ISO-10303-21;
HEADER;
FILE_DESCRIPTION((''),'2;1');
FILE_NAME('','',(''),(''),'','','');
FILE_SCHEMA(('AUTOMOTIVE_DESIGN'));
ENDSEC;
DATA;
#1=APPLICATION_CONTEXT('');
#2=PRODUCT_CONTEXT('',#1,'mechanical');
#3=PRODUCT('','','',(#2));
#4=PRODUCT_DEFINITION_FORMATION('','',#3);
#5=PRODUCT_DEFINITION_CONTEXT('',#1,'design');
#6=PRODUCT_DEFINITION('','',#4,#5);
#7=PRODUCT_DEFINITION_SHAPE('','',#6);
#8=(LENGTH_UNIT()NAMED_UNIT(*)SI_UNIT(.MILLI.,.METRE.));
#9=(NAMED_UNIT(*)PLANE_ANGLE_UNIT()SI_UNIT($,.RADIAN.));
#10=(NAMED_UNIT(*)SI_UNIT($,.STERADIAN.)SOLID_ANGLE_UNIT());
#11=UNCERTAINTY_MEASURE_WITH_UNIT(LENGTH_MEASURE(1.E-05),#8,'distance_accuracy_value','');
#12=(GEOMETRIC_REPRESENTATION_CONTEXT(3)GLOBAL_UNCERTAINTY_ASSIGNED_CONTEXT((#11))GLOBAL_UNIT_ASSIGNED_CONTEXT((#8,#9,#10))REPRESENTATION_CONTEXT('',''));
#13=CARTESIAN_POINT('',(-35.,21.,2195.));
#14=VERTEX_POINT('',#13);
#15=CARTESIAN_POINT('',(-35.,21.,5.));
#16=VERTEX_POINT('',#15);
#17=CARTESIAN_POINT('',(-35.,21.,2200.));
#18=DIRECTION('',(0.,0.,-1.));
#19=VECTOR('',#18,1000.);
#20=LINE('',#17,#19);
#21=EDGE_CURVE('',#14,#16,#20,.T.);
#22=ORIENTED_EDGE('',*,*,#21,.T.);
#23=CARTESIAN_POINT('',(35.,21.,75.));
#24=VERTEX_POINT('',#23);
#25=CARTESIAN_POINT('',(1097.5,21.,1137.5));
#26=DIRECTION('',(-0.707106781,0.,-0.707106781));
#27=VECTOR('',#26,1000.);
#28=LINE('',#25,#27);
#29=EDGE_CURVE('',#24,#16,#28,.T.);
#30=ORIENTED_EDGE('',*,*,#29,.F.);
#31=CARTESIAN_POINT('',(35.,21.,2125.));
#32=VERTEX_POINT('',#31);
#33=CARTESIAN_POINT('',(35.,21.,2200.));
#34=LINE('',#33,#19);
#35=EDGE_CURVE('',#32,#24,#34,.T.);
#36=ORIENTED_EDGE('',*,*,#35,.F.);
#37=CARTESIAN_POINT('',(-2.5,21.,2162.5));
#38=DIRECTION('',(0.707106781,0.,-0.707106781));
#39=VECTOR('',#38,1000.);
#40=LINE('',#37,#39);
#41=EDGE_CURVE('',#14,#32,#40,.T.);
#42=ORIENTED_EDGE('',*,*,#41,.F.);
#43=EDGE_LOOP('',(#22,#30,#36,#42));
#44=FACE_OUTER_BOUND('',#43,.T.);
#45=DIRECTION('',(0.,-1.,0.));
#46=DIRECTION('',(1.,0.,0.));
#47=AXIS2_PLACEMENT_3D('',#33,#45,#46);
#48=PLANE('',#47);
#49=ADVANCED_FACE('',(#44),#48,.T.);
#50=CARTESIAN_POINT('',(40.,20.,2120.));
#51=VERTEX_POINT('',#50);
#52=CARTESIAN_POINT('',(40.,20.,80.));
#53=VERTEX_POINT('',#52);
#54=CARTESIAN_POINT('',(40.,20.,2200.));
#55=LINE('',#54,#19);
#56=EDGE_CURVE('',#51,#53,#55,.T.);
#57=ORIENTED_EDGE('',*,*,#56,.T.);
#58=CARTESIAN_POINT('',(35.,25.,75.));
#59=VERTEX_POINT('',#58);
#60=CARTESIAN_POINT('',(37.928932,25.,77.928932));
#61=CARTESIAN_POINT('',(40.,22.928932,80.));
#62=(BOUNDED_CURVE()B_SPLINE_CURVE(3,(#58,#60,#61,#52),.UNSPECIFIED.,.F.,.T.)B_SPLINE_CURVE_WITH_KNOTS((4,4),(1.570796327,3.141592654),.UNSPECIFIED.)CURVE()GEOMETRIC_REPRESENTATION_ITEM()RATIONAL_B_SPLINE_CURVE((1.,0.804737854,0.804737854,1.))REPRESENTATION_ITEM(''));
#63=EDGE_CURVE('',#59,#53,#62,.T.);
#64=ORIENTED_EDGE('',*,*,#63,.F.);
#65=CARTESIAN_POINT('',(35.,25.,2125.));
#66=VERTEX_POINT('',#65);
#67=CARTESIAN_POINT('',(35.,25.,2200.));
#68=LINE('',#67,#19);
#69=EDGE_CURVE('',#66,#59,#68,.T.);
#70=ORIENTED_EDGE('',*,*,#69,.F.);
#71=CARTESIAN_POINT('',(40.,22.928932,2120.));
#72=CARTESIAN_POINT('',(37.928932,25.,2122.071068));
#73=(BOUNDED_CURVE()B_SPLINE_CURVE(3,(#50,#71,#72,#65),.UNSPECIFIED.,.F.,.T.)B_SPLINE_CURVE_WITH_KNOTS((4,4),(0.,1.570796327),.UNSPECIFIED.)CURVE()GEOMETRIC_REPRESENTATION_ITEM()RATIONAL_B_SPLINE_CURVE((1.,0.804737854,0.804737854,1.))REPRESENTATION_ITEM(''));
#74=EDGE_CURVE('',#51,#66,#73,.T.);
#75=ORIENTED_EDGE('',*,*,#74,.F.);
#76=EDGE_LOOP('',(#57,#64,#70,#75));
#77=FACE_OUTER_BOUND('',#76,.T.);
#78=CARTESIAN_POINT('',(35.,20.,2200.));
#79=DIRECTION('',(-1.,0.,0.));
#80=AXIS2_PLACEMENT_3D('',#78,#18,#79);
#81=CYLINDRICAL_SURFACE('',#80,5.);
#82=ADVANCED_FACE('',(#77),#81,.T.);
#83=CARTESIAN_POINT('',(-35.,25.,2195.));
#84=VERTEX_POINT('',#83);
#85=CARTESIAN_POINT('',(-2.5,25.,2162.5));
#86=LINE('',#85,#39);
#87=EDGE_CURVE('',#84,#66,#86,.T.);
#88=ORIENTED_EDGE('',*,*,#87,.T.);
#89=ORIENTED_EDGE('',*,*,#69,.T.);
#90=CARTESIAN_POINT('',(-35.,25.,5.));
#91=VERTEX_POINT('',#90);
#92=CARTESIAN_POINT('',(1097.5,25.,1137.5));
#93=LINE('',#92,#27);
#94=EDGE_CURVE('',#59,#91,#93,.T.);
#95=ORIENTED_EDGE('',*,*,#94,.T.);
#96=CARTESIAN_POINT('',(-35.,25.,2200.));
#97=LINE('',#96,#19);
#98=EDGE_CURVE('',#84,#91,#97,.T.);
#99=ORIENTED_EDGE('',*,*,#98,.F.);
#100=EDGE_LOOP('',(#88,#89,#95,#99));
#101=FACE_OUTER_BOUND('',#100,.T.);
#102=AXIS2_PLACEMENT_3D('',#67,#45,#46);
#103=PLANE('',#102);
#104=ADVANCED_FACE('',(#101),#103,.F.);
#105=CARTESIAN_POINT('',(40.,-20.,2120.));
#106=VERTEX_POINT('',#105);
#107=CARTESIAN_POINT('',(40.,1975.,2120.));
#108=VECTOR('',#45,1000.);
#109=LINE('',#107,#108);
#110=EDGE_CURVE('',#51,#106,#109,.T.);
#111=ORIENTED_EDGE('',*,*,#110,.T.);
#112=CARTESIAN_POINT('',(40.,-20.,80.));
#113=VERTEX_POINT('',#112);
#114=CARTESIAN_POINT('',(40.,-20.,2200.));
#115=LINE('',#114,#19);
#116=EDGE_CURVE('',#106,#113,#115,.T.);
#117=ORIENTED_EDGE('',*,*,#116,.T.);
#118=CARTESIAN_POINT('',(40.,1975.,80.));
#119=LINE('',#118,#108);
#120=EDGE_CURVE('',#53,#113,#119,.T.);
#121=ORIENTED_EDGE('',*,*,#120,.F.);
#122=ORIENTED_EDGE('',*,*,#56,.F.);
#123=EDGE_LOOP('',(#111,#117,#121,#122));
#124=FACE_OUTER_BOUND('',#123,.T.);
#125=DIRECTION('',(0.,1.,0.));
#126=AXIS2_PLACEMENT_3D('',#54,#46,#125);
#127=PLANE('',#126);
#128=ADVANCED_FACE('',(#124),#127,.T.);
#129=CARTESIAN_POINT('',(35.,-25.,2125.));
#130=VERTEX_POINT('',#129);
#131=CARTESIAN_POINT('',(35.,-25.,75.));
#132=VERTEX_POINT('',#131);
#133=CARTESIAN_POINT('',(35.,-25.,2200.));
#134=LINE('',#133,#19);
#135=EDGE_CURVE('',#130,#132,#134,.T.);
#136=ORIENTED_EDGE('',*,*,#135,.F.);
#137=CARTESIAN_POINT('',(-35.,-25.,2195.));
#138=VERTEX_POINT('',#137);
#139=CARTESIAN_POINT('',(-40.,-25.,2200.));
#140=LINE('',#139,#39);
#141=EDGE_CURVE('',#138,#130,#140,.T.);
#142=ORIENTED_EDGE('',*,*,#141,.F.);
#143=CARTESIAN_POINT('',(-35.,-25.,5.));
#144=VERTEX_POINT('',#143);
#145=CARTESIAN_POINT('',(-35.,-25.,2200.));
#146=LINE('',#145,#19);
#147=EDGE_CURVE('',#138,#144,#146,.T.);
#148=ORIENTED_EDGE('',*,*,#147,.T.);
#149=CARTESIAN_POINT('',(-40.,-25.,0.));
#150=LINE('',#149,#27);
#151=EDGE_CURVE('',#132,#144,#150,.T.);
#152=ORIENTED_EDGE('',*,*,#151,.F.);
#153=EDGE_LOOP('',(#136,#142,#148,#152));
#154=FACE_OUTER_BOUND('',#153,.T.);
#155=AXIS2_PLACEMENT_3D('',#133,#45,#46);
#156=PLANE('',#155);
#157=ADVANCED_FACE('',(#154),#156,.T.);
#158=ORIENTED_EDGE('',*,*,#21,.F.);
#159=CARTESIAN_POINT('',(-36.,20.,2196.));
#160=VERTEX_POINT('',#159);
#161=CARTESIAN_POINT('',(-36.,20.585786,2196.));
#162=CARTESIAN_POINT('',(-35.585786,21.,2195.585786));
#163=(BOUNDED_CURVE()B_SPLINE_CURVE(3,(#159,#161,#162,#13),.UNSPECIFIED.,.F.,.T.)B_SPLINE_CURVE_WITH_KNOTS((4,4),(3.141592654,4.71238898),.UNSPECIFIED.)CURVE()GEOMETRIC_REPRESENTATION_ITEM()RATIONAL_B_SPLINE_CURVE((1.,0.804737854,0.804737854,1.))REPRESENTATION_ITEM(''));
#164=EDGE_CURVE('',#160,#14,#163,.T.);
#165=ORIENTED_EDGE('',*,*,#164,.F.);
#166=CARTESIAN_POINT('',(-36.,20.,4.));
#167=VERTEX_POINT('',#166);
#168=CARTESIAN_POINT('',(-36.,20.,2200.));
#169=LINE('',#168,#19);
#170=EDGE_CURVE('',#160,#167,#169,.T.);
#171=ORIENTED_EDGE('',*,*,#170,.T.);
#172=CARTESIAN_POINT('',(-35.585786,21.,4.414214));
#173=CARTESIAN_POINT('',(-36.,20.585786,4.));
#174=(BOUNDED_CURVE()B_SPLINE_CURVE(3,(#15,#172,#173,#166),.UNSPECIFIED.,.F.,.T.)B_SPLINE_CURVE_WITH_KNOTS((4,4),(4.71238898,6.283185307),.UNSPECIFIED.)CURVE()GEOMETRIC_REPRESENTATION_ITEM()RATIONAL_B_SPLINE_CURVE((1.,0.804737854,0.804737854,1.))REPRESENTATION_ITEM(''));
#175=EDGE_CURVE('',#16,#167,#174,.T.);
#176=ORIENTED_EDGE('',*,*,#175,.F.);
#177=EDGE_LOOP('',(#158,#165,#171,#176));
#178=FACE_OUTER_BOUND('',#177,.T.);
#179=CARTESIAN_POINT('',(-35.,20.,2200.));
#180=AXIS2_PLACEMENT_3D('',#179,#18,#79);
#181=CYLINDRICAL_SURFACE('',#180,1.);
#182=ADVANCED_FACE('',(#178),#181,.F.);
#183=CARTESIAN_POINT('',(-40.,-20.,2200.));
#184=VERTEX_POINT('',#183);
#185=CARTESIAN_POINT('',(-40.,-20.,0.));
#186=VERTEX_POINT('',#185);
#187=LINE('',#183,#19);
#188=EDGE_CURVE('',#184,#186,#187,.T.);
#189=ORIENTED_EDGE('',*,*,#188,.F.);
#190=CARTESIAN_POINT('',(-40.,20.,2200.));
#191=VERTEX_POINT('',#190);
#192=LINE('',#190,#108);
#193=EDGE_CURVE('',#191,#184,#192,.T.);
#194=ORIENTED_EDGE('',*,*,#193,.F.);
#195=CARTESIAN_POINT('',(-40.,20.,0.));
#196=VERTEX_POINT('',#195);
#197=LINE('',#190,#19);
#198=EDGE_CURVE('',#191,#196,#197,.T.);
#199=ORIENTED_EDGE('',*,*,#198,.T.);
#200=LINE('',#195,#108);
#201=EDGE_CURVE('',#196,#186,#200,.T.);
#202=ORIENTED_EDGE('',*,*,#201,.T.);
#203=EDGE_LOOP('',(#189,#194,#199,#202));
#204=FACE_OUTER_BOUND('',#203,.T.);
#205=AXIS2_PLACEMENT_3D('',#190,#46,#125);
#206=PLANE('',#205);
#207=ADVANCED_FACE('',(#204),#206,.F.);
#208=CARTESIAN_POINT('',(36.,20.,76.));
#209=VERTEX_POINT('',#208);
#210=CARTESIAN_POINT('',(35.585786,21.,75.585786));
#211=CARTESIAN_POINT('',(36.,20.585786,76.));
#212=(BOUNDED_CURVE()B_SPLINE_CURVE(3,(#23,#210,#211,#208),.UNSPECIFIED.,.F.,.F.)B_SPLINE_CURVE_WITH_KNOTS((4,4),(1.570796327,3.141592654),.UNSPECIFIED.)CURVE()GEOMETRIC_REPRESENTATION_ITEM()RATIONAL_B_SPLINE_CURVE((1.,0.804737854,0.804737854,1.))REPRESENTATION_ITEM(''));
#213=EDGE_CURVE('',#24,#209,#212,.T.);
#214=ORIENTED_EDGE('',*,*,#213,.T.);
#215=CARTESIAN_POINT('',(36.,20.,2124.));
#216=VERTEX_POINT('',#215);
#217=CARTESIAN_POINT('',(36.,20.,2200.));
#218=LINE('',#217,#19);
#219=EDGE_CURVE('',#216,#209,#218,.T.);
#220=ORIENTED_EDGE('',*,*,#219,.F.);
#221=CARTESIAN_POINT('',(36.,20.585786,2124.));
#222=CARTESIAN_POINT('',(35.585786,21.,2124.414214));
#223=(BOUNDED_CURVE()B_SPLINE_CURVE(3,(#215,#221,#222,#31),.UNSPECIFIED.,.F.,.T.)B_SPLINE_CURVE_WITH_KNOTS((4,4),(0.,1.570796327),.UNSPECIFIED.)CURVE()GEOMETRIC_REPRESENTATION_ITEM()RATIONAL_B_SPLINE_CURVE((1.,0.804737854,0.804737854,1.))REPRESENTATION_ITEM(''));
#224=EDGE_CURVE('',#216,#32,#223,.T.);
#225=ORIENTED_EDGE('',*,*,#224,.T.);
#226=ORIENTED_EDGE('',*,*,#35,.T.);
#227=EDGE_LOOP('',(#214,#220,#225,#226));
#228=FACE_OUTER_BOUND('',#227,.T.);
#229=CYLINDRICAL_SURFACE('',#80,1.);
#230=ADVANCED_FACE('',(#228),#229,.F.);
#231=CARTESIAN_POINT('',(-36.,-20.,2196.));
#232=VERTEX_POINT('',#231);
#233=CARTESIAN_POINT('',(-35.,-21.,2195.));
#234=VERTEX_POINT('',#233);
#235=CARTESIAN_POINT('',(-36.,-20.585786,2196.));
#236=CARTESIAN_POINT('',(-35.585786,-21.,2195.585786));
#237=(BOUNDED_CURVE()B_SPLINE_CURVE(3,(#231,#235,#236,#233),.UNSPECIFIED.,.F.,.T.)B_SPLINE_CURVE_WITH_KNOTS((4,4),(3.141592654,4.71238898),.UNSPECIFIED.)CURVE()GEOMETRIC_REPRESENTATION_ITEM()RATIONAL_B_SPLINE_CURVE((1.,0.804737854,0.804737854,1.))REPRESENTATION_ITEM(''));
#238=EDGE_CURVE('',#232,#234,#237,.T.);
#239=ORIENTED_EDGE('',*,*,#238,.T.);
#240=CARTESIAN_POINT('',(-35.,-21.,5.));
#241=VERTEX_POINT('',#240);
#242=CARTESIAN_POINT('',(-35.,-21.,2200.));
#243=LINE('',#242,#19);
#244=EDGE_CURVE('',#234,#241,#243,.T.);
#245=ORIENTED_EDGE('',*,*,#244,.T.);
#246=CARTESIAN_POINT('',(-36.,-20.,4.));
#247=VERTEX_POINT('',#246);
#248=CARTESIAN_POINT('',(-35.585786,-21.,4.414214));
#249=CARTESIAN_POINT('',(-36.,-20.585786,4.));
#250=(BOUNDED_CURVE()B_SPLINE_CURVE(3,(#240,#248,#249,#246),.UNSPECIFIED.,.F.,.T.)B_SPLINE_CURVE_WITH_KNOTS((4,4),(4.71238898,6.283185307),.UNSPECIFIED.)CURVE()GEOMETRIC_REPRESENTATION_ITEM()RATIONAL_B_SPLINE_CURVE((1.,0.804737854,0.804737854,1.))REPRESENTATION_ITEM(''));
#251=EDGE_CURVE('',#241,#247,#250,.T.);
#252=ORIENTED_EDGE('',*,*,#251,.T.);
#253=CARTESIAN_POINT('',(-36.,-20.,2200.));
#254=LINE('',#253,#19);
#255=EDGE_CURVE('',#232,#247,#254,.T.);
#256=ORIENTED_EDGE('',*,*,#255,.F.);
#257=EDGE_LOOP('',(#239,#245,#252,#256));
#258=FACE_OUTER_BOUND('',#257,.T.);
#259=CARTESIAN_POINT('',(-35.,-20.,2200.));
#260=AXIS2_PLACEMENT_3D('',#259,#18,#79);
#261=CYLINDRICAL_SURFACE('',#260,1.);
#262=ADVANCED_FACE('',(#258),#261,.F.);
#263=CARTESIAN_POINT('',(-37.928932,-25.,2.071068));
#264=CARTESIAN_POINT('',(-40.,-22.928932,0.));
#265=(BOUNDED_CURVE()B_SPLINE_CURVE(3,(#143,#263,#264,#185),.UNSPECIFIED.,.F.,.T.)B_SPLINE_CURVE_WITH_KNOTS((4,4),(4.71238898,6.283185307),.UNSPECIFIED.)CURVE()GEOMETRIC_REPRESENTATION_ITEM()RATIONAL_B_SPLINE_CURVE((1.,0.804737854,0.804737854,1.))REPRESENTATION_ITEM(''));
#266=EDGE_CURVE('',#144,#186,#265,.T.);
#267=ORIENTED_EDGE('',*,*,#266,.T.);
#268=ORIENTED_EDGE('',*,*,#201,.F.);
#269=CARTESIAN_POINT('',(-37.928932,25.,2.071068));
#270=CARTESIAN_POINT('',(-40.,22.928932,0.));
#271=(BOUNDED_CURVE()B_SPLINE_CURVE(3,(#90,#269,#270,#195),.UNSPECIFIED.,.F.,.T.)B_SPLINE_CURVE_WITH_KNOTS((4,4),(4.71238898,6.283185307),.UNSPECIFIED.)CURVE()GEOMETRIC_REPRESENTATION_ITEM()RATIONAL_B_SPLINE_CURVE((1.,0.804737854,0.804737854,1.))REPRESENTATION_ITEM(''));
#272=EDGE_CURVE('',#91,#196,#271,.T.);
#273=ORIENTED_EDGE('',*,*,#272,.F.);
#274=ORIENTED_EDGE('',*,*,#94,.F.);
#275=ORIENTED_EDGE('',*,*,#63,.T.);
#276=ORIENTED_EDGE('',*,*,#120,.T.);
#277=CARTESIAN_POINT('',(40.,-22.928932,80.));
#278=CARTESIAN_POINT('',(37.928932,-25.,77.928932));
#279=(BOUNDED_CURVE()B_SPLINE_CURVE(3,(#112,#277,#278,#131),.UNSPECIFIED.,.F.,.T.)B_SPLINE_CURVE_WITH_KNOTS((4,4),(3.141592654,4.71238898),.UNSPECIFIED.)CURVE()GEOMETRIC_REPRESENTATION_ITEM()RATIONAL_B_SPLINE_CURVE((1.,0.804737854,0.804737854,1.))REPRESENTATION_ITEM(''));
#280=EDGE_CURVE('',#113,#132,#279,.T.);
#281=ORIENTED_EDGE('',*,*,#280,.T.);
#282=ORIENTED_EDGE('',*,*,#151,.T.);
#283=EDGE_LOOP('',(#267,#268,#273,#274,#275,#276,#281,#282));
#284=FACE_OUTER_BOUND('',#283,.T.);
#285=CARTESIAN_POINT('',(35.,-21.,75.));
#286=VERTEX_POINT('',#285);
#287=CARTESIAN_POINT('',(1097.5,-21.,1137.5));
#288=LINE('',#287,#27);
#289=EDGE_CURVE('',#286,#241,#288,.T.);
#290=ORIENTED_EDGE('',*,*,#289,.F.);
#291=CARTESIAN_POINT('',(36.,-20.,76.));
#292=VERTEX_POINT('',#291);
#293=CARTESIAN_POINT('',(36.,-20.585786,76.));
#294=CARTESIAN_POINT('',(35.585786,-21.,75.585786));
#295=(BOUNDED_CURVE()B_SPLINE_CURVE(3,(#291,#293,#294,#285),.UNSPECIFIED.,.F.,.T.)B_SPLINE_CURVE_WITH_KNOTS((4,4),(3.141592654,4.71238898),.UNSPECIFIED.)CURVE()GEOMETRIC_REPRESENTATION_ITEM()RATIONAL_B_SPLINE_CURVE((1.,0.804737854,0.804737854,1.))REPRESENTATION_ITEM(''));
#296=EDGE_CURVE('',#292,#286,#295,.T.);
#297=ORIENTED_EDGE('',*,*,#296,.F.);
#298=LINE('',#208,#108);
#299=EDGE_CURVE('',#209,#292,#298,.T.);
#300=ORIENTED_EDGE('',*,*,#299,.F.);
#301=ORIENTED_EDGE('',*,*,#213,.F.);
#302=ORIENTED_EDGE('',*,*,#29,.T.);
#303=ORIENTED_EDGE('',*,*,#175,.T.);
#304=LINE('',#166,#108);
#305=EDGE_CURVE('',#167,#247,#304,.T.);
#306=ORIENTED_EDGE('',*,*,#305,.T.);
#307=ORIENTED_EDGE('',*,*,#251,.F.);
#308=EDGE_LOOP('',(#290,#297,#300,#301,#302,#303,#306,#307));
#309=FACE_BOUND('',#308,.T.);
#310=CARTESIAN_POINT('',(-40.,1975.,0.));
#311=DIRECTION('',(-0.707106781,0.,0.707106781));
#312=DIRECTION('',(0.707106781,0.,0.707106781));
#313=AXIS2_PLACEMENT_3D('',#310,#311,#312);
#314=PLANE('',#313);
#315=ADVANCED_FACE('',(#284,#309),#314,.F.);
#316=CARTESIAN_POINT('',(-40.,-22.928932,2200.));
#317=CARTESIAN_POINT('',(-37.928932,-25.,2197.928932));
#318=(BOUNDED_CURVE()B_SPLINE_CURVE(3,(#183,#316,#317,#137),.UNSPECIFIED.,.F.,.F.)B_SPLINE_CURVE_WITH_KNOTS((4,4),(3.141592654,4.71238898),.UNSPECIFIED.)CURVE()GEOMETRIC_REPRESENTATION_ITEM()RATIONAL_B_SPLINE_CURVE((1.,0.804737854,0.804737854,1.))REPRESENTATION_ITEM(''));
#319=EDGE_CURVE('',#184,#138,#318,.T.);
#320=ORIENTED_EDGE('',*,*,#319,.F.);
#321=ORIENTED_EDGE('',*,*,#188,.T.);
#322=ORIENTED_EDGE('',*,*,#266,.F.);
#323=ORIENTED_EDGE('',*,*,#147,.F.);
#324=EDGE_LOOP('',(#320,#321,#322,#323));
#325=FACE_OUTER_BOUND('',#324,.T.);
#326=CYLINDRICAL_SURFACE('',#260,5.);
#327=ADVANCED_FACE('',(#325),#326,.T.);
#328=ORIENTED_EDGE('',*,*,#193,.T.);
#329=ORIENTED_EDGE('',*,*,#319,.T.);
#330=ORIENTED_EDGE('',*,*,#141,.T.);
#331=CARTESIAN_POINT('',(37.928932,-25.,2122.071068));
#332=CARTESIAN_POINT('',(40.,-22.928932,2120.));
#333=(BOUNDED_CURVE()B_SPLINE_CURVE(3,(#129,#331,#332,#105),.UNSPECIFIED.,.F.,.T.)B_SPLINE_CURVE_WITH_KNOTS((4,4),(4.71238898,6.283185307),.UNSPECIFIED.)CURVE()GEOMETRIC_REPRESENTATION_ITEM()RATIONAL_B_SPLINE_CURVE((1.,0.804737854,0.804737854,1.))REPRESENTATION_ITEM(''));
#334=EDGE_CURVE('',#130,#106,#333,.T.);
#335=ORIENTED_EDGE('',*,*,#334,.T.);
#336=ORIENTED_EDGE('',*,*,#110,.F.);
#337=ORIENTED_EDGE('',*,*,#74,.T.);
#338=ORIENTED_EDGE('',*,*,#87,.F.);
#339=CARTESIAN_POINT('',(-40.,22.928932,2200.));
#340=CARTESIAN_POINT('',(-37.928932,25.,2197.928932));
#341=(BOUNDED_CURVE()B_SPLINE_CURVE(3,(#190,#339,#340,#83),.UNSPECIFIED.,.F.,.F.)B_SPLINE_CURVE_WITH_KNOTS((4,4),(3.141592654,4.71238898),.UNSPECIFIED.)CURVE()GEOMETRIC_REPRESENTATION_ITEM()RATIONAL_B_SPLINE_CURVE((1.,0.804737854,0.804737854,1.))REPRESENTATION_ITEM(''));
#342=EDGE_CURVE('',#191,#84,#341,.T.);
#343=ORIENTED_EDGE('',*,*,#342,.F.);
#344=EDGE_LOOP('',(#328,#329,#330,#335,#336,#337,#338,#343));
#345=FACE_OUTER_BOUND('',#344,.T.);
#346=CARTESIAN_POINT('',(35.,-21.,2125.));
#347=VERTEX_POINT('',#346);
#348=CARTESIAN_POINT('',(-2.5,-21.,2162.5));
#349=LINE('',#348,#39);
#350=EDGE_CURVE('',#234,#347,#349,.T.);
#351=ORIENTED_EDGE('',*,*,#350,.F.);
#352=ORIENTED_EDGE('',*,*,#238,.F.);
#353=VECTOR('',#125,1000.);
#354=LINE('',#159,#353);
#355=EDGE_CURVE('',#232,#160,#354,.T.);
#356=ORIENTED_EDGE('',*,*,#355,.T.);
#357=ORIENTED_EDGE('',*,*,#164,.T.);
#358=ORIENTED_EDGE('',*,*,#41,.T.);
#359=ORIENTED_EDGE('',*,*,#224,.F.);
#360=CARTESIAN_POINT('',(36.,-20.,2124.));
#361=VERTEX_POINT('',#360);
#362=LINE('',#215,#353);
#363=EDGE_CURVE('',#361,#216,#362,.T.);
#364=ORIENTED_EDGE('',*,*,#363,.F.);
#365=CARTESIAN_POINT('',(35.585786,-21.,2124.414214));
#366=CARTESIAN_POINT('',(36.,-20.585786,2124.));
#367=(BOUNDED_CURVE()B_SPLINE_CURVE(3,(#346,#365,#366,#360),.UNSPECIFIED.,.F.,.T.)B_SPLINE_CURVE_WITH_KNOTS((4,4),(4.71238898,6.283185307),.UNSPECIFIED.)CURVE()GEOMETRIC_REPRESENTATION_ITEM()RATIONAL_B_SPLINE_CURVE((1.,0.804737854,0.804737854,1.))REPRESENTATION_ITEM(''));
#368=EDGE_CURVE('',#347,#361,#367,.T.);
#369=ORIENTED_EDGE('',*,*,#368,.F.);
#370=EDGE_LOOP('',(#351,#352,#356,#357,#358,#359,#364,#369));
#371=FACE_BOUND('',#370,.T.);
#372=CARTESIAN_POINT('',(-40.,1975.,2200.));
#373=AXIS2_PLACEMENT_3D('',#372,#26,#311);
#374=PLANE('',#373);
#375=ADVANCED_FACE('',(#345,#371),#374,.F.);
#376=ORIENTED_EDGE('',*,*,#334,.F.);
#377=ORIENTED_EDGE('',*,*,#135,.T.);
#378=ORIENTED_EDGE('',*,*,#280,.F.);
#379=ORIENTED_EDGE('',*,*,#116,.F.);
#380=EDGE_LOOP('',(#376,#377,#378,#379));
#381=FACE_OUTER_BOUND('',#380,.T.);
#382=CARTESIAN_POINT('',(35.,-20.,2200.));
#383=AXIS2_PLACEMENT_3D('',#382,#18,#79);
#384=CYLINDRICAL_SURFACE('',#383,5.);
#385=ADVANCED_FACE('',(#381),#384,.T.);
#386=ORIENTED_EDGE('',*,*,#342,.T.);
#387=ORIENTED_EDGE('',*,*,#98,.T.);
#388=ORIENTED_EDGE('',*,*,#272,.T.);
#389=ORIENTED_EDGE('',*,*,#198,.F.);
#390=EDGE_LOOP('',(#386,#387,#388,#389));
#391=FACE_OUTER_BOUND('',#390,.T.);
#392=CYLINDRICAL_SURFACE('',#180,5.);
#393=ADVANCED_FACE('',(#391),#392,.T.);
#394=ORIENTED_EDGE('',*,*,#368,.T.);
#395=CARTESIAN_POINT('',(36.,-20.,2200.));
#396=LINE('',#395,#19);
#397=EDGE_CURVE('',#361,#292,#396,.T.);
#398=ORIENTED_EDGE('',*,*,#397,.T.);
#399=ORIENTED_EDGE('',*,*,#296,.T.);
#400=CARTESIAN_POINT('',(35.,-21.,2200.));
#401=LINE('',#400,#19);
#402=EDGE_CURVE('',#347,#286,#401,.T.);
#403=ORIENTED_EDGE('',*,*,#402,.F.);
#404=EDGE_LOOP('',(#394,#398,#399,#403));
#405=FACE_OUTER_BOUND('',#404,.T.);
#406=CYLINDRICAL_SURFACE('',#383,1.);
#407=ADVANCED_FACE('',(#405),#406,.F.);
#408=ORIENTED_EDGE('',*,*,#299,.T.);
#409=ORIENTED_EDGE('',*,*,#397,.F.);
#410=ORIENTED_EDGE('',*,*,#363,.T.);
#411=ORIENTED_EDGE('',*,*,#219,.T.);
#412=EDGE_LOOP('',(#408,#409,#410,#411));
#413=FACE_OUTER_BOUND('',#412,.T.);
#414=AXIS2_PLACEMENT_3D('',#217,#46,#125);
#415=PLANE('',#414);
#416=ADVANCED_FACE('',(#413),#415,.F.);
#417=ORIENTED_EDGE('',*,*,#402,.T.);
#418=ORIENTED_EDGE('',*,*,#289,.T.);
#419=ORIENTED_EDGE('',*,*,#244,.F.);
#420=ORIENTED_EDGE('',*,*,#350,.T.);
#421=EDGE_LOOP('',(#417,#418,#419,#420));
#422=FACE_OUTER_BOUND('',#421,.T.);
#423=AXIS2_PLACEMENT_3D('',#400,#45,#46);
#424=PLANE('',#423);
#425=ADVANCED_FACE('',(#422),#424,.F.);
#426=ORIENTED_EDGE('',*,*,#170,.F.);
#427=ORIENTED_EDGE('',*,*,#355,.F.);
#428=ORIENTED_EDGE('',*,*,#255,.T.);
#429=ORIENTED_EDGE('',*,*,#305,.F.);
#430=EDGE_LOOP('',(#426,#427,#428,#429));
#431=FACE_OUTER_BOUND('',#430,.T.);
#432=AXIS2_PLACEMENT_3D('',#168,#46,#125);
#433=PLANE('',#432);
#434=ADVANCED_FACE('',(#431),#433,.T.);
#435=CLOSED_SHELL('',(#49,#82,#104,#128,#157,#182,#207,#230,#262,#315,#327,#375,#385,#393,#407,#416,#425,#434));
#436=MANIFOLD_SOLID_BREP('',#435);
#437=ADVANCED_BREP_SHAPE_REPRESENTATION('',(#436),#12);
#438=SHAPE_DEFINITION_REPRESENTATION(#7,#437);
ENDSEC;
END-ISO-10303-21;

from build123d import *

# Parameters (mm, degrees)
BOSS_EXTRUDE1_DEPTH = 2200
SHELL1_T            = -4
CUT_EXTRUDE2_DEPTH  = 2000


with BuildPart() as part:
    # Sketch1 → Boss-Extrude1 (new body)
    with BuildSketch(Plane.XY):
        with BuildLine():
            Line((35, 25), (-35, 25))
            ThreePointArc((-35, 25), (-38.535533906, 23.535533906), (-40, 20))
            Line((-40, 20), (-40, -20))
            ThreePointArc((-40, -20), (-38.535533906, -23.535533906), (-35, -25))
            Line((-35, -25), (35, -25))
            ThreePointArc((35, -25), (38.535533906, -23.535533906), (40, -20))
            Line((40, -20), (40, 20))
            ThreePointArc((40, 20), (38.535533906, 23.535533906), (35, 25))
        make_face()
    extrude(amount=BOSS_EXTRUDE1_DEPTH)

    # Shell1
    shell1_openings = [part.faces().sort_by_distance(p)[0] for p in [
        (0, 0, 2200),
        (0, 0, 0),
    ]]
    offset(amount=SHELL1_T, openings=shell1_openings, kind=Kind.INTERSECTION)

    # Sketch3 → Cut-Extrude2 (cut)
    with BuildSketch(Plane.XZ.offset(25)):
        Polygon((-40, 2200), (40, 2120), (40, 2200), align=None)
        Polygon((40, 80), (40, 0), (-40, 0), align=None)
    extrude(amount=-CUT_EXTRUDE2_DEPTH, mode=Mode.SUBTRACT)


solid = part.part
